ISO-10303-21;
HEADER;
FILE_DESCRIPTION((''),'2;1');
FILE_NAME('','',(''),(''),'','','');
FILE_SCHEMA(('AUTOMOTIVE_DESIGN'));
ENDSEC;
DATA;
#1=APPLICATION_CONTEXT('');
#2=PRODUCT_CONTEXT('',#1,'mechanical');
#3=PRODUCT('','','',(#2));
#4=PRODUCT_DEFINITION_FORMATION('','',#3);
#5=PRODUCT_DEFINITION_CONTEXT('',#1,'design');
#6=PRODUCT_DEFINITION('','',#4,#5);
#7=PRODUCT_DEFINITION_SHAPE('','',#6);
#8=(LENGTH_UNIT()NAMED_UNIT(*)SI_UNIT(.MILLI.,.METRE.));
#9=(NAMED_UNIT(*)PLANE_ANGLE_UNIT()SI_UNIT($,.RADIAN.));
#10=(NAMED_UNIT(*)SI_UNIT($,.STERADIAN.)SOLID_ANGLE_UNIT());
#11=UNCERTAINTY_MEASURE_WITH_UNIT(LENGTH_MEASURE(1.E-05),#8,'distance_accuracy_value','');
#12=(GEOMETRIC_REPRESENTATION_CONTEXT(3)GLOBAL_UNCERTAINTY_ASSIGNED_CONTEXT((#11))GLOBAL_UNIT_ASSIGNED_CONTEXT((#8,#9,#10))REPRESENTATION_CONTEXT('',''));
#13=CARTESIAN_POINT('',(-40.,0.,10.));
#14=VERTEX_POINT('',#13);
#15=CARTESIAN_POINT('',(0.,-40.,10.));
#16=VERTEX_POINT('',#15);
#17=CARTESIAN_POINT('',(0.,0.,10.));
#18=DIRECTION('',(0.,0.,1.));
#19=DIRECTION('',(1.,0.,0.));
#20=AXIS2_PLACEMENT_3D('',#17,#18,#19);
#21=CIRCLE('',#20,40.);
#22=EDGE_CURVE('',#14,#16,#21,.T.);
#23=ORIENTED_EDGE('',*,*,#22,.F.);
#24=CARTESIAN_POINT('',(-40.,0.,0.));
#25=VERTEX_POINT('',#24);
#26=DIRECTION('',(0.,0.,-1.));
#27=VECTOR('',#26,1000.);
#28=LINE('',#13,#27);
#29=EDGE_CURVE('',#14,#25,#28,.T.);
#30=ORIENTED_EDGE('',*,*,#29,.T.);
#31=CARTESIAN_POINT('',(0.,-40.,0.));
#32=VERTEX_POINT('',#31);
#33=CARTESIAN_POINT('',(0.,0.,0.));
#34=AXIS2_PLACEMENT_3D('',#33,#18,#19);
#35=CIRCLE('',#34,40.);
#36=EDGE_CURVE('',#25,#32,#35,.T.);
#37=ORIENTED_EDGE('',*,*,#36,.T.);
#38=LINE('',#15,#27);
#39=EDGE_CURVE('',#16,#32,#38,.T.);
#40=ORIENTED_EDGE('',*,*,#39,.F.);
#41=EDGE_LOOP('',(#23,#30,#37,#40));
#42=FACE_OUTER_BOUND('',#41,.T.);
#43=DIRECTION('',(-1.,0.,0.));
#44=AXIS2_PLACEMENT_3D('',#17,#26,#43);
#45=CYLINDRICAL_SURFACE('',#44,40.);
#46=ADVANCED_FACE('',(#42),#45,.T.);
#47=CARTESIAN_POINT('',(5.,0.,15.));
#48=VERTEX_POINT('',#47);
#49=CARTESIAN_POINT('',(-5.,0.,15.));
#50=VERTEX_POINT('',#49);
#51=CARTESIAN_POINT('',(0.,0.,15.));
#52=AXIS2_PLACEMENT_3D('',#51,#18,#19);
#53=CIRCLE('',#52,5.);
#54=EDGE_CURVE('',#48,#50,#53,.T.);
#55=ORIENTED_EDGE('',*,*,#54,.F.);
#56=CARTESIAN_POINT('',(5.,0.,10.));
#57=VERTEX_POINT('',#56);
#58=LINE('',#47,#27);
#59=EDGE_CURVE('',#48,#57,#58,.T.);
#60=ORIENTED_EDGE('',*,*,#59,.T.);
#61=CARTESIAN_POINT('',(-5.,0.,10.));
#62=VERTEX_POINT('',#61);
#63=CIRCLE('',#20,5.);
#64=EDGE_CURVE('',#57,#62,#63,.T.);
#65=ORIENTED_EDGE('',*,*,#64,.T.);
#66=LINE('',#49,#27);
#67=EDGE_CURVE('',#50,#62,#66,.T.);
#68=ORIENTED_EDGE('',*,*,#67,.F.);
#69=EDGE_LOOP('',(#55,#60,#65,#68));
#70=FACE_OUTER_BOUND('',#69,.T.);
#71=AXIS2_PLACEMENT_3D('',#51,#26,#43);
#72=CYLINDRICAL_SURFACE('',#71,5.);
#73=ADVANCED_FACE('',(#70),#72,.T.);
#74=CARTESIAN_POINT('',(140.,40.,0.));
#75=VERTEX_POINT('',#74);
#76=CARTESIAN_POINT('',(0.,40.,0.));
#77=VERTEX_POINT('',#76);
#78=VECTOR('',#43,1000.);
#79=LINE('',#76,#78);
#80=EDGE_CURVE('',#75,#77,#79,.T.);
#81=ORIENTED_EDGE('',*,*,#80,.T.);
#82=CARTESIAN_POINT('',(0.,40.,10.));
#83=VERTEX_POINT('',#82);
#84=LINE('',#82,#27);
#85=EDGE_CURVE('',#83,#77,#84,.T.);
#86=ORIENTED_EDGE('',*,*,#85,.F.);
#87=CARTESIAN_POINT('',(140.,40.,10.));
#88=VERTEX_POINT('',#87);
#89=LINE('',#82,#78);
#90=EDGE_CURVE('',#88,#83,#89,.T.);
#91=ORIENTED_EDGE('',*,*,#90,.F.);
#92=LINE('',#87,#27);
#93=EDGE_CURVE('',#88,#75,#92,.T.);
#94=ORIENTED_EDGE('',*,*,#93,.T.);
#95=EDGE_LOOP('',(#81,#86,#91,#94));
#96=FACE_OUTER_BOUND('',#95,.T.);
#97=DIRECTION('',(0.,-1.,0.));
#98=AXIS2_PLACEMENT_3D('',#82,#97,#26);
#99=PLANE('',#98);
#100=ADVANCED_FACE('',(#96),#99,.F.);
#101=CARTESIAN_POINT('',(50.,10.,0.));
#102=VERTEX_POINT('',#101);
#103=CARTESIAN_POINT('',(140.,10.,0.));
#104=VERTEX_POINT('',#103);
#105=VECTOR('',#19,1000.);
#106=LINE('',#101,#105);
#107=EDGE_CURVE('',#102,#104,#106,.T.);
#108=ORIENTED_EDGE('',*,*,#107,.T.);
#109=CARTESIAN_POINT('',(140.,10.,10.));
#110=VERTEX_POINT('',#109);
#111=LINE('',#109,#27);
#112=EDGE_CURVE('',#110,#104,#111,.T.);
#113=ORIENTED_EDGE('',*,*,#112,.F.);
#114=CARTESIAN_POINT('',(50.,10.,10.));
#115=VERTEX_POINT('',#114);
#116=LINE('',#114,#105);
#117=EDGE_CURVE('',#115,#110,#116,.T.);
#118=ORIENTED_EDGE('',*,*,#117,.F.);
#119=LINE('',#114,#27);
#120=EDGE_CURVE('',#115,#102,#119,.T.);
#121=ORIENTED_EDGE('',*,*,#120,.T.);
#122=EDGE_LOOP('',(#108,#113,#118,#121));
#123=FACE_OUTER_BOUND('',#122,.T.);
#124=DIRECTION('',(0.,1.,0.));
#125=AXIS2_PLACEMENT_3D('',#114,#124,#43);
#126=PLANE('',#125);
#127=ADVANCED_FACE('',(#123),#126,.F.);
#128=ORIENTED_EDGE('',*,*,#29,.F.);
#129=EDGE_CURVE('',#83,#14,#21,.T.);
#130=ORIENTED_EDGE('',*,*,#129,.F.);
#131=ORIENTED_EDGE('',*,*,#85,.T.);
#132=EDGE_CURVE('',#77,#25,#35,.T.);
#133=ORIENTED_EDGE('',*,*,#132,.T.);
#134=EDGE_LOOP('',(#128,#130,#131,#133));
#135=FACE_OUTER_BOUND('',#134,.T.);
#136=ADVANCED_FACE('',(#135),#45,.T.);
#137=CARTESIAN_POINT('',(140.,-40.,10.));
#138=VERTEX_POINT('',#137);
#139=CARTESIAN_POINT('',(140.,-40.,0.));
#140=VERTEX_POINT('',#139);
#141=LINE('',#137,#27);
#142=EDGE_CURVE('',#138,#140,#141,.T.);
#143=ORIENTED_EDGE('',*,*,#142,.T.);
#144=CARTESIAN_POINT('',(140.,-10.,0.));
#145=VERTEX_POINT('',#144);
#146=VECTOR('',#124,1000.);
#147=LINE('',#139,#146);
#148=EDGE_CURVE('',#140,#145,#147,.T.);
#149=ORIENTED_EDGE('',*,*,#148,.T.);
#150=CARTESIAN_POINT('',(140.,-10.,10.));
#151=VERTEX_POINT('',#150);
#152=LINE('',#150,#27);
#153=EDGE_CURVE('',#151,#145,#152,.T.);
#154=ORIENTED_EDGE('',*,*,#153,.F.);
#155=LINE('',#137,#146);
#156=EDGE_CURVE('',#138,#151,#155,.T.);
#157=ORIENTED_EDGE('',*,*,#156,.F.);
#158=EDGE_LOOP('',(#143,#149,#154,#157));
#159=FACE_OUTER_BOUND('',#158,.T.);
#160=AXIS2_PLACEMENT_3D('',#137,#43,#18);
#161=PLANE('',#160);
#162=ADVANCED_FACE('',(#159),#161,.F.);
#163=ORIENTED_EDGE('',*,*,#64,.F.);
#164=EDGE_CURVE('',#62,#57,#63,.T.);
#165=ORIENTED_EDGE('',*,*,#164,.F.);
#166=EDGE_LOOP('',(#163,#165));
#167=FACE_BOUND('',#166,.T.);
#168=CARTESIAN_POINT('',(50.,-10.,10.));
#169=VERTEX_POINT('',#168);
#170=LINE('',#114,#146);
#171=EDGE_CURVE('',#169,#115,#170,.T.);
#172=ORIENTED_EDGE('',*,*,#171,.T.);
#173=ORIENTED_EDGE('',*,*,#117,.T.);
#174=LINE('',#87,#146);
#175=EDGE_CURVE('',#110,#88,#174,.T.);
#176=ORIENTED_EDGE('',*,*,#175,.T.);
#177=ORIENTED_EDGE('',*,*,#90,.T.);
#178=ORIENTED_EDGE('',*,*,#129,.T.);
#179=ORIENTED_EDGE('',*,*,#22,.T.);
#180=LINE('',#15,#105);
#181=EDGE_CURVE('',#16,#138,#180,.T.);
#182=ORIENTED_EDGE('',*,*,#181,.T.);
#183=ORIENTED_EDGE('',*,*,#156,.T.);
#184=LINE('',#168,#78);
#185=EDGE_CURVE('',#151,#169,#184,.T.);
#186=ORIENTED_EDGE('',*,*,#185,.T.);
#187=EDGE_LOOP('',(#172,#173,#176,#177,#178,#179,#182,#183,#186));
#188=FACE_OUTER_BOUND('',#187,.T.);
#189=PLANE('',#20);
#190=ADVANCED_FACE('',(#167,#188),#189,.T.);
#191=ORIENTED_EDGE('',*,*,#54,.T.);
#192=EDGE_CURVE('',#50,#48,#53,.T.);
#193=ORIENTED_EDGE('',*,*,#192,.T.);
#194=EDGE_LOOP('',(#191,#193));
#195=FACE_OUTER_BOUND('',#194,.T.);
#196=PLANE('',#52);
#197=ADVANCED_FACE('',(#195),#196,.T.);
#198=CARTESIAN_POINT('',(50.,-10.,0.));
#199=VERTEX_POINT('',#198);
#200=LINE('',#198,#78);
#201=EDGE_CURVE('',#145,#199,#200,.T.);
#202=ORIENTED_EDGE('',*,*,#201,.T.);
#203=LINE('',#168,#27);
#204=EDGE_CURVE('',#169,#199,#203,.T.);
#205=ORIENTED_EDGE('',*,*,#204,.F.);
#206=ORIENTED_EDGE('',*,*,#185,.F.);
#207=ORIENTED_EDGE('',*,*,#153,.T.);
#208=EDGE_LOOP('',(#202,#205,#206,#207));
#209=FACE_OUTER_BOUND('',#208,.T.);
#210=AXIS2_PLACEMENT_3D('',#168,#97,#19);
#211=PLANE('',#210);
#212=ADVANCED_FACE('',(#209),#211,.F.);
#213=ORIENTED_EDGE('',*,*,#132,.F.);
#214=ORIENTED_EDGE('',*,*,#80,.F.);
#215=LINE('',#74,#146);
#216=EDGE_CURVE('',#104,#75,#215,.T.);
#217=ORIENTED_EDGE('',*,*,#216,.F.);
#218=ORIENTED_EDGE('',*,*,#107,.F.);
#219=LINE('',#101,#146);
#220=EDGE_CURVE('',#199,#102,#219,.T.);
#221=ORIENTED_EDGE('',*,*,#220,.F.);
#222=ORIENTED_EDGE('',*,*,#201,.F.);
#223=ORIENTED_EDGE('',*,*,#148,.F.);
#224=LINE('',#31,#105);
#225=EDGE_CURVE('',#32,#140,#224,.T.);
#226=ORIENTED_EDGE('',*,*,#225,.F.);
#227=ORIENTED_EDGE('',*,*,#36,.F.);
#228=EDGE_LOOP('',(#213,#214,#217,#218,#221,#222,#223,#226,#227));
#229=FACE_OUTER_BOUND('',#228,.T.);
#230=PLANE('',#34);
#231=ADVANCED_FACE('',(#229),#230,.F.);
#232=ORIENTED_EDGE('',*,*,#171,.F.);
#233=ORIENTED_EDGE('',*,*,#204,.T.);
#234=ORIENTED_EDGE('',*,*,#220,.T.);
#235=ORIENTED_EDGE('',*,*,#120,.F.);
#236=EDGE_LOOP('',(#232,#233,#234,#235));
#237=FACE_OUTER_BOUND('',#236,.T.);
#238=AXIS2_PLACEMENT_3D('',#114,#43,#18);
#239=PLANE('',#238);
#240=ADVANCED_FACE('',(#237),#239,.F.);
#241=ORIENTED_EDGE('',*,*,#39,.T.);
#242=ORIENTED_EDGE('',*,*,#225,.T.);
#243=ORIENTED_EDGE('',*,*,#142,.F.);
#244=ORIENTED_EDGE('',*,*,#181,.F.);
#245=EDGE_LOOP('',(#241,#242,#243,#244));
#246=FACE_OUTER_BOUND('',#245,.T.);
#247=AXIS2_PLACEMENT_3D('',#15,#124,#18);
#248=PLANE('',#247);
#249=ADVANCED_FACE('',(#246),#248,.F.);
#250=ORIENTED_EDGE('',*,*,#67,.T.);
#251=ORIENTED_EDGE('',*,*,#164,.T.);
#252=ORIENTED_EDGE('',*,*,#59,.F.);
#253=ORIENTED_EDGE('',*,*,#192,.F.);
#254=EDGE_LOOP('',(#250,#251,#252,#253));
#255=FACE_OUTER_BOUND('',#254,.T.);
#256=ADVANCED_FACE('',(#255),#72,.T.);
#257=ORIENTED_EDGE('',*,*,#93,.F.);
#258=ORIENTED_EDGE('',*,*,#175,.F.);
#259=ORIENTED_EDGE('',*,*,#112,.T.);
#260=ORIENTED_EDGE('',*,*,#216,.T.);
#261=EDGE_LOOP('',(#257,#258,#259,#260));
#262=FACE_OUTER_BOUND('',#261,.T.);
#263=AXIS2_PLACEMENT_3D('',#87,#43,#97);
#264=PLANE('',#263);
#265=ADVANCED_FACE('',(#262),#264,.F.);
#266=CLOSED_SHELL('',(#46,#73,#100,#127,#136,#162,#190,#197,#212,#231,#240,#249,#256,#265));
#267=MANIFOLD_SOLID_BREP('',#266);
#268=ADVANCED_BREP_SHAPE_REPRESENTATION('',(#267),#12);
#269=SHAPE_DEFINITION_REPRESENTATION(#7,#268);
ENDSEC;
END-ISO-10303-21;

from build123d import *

# Parameters (mm, degrees)
BASE_EXTRUDE_DEPTH  = 10
SKETCH2_R           = 5
BOSS_EXTRUDE1_DEPTH = 5


with BuildPart() as part:
    # Sketch1 → Base-Extrude (new body)
    with BuildSketch(Plane.XY):
        with BuildLine():
            Line((0, 40), (140, 40))
            Line((140, 40), (140, 10))
            Line((140, 10), (50, 10))
            Line((50, 10), (50, -10))
            Line((50, -10), (140, -10))
            Line((140, -10), (140, -40))
            Line((140, -40), (0, -40))
            ThreePointArc((0, -40), (-40, 0), (0, 40))
        make_face()
    extrude(amount=BASE_EXTRUDE_DEPTH)

    # Sketch2 → Boss-Extrude1 (add)
    with BuildSketch(Plane.XY.offset(10)):
        Circle(SKETCH2_R)
    extrude(amount=BOSS_EXTRUDE1_DEPTH)


solid = part.part
